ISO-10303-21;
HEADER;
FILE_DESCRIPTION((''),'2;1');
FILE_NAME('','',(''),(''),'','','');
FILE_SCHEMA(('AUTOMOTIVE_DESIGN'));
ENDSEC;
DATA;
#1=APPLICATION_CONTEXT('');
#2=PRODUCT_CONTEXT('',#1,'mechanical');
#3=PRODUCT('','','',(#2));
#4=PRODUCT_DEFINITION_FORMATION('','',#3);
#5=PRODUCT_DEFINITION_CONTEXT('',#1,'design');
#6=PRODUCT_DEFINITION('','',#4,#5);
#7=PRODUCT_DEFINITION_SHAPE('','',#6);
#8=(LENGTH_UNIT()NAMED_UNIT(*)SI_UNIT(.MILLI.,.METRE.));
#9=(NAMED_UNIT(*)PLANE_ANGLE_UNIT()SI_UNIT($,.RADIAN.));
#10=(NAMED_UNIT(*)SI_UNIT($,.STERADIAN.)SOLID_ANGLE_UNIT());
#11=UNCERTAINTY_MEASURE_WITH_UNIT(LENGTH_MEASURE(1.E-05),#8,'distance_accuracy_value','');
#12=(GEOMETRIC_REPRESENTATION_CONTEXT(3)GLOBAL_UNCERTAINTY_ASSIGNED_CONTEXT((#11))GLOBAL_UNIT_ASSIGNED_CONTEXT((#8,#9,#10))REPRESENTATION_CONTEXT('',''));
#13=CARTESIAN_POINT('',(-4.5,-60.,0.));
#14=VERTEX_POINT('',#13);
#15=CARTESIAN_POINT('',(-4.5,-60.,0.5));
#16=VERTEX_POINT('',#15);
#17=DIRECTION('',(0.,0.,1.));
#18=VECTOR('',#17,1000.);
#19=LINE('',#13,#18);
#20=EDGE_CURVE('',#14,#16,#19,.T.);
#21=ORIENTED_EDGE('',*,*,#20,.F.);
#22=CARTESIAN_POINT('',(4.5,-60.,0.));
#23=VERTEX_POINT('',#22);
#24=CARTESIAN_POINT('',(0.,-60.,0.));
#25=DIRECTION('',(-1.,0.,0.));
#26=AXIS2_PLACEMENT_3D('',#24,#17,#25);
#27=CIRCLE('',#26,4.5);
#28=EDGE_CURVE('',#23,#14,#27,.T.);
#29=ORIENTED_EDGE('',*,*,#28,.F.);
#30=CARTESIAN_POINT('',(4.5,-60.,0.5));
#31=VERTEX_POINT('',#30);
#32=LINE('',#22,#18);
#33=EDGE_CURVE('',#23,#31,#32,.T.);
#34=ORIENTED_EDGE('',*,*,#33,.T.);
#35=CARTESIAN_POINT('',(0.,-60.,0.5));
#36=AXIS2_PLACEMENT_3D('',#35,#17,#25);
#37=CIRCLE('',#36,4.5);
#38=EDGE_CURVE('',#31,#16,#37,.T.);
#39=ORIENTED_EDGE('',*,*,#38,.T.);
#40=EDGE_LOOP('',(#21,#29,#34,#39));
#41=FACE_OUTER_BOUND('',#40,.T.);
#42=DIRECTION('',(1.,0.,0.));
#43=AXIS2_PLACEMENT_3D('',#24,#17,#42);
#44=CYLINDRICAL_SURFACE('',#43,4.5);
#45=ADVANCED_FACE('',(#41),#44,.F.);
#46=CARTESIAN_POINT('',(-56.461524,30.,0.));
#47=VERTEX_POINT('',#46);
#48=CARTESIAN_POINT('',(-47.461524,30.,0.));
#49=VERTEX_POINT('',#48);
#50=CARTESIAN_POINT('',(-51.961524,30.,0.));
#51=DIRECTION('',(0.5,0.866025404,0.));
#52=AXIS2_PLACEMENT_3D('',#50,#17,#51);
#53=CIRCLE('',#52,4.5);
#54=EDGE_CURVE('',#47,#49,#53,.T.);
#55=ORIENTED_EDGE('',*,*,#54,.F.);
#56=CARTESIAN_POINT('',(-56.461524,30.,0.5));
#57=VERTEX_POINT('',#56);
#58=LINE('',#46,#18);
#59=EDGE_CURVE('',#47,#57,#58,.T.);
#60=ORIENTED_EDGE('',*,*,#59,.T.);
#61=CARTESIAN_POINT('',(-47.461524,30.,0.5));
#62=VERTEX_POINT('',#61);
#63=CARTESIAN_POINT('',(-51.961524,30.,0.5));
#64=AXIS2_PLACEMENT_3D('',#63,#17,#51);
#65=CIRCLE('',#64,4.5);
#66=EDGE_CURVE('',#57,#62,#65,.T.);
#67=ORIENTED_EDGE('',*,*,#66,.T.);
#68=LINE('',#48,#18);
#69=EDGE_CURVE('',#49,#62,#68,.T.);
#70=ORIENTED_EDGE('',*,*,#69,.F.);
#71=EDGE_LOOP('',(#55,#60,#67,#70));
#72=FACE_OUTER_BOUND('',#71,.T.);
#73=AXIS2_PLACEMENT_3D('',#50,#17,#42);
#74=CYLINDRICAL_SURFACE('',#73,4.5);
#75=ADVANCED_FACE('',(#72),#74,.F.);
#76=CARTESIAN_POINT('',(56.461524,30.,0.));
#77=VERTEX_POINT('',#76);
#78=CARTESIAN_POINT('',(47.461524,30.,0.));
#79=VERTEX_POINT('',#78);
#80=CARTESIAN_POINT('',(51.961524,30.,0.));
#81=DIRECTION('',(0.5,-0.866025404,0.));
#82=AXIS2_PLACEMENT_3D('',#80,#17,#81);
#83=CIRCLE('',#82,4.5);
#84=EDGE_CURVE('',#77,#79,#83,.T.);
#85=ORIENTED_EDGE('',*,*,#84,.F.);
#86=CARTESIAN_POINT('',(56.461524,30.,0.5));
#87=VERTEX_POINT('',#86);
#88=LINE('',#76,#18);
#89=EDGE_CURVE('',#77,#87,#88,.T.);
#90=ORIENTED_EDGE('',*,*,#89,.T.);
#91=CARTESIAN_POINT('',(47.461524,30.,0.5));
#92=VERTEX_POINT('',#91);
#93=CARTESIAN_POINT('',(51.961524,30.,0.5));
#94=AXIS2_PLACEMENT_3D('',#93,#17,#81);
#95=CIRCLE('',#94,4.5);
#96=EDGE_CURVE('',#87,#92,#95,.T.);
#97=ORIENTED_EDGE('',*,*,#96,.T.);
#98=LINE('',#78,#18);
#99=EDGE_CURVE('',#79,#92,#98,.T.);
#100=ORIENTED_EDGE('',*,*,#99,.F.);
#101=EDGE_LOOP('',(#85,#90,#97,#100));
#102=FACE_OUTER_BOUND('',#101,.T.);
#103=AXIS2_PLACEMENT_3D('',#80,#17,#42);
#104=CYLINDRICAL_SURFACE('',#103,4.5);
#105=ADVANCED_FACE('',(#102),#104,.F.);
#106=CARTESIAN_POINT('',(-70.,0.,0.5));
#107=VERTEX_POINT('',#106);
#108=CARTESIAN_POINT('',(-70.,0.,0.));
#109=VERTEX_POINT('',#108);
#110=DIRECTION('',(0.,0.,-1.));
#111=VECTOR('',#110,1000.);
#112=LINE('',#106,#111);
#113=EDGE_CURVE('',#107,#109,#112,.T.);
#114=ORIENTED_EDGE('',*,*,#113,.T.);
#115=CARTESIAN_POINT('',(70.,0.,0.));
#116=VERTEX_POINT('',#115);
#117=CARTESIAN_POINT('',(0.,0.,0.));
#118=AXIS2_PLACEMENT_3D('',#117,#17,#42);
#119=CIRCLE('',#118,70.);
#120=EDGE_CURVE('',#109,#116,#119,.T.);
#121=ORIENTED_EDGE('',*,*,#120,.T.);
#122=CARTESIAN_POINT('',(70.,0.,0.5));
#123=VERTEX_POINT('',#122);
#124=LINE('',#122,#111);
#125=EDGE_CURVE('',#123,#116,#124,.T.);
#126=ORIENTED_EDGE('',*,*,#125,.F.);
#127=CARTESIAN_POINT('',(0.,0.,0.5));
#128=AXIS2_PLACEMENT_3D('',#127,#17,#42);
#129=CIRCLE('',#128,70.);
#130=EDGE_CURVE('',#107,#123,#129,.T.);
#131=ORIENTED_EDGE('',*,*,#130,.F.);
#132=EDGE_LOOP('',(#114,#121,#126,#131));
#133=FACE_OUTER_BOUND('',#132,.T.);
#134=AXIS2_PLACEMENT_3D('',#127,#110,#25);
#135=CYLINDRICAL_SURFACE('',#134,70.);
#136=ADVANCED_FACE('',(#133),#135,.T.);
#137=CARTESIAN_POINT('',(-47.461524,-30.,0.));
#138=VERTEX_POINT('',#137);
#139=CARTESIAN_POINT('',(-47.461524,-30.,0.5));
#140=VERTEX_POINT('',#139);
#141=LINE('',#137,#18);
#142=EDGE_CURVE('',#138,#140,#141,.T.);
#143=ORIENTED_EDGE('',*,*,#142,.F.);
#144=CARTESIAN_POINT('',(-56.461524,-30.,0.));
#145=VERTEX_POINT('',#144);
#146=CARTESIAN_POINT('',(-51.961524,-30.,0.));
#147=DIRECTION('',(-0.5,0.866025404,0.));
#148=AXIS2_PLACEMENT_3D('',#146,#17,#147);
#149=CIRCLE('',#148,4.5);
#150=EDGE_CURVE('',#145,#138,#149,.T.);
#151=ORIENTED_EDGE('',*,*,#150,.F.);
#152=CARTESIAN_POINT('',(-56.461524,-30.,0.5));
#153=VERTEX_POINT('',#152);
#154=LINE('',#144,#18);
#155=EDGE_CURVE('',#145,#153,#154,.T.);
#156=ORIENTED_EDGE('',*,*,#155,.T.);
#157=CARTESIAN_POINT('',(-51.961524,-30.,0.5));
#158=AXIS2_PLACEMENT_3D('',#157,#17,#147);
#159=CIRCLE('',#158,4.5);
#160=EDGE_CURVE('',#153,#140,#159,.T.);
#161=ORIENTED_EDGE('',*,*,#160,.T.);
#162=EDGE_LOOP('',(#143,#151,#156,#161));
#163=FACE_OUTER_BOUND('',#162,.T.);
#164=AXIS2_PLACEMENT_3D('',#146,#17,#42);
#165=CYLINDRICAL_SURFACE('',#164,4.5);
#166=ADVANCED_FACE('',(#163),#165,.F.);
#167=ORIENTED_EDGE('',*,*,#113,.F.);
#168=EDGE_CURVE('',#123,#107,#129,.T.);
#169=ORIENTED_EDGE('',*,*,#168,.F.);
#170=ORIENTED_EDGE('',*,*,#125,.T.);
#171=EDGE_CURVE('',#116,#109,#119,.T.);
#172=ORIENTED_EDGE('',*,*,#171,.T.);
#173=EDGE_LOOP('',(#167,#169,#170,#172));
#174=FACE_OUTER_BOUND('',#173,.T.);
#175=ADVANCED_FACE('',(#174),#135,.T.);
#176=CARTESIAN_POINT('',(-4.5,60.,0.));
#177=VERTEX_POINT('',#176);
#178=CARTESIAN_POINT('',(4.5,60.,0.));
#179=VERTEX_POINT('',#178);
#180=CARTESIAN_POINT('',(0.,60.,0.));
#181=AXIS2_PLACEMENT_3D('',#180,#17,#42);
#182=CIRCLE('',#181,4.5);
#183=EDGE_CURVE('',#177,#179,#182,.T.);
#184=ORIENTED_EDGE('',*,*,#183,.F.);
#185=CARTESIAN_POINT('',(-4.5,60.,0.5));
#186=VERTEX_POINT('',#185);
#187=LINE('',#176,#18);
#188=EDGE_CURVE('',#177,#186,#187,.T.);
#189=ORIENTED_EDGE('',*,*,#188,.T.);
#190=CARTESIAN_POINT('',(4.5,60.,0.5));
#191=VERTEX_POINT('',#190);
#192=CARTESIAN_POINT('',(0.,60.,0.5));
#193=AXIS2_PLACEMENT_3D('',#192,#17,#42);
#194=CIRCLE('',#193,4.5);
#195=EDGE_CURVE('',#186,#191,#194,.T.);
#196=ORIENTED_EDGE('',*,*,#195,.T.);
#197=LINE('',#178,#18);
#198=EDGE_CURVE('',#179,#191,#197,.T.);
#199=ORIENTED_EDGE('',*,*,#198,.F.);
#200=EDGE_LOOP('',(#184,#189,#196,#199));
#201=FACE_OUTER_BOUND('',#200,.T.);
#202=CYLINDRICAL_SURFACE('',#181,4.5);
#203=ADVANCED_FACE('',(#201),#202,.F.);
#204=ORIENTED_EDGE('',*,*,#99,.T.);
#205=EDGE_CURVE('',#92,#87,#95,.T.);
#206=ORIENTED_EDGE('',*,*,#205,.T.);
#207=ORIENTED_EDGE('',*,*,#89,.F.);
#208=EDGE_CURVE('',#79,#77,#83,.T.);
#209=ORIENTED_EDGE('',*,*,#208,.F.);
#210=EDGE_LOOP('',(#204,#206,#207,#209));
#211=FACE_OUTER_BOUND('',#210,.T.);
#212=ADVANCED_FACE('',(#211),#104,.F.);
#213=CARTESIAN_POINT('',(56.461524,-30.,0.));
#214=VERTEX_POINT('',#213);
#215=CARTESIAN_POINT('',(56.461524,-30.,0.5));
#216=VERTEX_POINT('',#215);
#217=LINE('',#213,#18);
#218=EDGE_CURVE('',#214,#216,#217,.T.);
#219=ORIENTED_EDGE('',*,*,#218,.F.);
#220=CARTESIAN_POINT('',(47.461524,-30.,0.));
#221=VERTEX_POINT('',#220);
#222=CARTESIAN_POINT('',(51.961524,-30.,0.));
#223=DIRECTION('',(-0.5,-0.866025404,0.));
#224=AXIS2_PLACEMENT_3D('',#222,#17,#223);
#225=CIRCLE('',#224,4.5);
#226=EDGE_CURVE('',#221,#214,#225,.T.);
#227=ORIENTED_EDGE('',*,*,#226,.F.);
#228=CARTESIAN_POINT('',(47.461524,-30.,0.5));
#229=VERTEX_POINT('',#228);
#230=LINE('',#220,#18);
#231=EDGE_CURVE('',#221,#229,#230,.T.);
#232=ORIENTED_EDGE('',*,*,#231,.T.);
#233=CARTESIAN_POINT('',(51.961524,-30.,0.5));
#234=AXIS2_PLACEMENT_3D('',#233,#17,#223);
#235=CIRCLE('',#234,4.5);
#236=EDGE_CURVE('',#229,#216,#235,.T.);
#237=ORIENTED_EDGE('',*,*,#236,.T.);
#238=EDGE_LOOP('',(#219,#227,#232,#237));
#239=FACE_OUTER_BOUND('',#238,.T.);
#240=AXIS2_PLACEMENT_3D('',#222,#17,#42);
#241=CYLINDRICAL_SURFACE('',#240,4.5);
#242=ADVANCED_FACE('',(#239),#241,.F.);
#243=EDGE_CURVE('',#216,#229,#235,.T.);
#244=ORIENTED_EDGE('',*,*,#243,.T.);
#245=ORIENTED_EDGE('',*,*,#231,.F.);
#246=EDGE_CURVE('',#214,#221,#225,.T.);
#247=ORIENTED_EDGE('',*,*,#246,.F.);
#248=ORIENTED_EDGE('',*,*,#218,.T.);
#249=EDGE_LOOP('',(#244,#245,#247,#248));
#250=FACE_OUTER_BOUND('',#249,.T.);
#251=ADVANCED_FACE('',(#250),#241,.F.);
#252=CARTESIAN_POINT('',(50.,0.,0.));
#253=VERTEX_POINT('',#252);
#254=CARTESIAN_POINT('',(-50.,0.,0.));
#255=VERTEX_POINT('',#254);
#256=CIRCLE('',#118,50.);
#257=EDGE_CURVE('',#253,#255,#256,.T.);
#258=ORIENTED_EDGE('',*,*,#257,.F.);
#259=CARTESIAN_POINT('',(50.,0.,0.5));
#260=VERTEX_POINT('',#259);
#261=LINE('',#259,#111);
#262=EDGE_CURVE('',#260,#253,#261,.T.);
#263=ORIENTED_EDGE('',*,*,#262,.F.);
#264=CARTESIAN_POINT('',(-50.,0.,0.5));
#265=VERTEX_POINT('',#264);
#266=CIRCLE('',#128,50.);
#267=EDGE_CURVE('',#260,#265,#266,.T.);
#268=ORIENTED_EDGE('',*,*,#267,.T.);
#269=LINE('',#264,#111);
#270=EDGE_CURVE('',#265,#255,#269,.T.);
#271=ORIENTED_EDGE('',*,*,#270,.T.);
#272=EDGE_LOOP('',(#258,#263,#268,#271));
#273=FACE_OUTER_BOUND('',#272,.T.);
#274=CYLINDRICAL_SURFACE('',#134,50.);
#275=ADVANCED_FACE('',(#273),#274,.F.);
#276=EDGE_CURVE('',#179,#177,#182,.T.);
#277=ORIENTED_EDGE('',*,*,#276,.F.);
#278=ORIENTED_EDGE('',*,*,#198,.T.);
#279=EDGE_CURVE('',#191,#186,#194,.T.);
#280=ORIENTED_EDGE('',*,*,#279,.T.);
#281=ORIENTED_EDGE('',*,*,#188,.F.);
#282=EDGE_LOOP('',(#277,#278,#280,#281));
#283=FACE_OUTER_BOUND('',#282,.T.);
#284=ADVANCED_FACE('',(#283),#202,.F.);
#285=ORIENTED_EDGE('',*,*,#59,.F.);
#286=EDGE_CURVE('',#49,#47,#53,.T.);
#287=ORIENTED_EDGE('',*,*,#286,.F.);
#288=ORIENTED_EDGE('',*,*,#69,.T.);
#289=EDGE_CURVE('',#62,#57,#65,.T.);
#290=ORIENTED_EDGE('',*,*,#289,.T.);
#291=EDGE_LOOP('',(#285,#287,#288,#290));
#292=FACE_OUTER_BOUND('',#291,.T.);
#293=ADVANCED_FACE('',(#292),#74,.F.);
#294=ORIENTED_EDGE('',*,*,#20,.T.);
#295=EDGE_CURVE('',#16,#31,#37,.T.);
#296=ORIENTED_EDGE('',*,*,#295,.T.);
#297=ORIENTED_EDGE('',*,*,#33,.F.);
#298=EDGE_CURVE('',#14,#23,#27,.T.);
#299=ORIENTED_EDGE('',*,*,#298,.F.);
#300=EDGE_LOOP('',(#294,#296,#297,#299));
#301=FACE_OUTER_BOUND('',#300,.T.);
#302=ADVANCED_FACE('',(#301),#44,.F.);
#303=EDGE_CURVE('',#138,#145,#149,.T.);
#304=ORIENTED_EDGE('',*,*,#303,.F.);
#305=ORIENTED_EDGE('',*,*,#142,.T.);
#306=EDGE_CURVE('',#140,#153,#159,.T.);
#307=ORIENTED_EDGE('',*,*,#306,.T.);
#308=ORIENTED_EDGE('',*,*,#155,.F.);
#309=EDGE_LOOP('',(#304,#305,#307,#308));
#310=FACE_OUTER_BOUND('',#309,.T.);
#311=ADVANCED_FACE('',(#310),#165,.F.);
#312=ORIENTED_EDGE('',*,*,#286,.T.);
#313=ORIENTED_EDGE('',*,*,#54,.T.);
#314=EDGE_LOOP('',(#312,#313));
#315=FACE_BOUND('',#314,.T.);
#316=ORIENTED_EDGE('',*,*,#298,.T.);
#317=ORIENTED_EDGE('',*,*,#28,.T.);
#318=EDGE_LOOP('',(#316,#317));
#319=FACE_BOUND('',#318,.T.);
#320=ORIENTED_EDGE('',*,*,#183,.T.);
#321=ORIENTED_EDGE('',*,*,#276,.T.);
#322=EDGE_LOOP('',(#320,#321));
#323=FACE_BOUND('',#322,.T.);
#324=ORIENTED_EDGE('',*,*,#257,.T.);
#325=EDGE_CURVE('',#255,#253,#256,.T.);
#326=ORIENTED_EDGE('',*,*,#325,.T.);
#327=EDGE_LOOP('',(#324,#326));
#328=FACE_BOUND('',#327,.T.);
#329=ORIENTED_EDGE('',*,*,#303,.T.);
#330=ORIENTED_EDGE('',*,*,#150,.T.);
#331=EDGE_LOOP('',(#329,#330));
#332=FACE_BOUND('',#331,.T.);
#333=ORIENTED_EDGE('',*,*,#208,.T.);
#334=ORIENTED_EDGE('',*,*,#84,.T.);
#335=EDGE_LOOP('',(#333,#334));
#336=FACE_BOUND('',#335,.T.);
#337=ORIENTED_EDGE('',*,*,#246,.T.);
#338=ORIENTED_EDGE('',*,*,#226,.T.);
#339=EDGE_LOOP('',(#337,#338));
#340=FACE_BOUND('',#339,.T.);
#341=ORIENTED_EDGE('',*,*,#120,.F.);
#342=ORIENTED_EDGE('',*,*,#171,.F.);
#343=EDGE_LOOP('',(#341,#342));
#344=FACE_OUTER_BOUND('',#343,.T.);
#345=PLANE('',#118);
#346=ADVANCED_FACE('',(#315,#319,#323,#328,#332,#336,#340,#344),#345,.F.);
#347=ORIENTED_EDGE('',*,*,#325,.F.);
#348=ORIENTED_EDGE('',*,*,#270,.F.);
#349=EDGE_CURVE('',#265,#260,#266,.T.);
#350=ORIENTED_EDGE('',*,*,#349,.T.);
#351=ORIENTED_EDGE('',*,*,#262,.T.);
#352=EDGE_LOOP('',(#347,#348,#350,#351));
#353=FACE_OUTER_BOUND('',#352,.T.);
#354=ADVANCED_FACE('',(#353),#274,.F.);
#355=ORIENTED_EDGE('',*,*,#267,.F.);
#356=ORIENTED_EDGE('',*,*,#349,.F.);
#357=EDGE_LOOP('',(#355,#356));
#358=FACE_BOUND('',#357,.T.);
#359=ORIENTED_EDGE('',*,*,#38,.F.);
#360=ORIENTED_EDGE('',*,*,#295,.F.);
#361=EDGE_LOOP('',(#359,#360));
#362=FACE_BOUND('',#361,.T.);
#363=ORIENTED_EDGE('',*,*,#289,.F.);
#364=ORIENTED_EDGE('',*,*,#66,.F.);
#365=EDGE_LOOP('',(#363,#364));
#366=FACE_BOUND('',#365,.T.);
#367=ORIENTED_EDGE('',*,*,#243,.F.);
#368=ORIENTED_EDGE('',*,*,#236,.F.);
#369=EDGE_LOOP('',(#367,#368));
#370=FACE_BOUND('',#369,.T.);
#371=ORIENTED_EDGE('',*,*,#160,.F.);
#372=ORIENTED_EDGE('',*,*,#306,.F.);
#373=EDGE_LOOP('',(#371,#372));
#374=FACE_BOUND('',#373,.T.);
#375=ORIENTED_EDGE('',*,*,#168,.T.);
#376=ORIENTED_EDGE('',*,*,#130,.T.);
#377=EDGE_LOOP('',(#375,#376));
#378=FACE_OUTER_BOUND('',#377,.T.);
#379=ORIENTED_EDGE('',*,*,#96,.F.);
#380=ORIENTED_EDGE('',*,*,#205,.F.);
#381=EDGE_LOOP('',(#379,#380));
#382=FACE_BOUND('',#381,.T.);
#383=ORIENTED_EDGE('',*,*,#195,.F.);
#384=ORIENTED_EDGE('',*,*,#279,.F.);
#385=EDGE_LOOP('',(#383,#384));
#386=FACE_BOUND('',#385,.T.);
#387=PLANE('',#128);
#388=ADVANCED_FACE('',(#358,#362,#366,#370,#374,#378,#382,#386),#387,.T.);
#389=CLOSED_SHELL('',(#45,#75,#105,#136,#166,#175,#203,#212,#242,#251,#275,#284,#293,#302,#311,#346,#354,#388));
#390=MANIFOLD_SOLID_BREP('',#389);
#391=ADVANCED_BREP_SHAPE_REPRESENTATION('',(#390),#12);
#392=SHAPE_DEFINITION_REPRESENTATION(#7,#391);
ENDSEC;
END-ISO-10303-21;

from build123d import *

# Parameters (mm, degrees)
SKETCH1_R           = 70
SKETCH1_R_2         = 50
BOSS_EXTRUDE1_DEPTH = 0.5
SKETCH2_R           = 4.5
CUT_EXTRUDE1_DEPTH  = 99.996212049
CIRPATTERN1_COUNT   = 6


with BuildPart() as part:
    # Sketch1 → Boss-Extrude1 (new body)
    with BuildSketch(Plane.XY):
        Circle(SKETCH1_R)
        Circle(SKETCH1_R_2, mode=Mode.SUBTRACT)
    extrude(amount=BOSS_EXTRUDE1_DEPTH)

    # Sketch2 → Cut-Extrude1 (cut, through all)
    with BuildSketch(Plane.XY.offset(0.5)):
        with Locations((0, 60)):
            Circle(SKETCH2_R)
    cut_extrude1 = extrude(amount=-CUT_EXTRUDE1_DEPTH, mode=Mode.SUBTRACT)

    # CirPattern1: Cut-Extrude1 ×6 about axis
    cirpattern1_axis = Axis((0, 0, 0), (0, 0, 1))
    for i in range(1, CIRPATTERN1_COUNT):
        add(cut_extrude1.rotate(cirpattern1_axis, i * 360 / CIRPATTERN1_COUNT), mode=Mode.SUBTRACT)


solid = part.part
